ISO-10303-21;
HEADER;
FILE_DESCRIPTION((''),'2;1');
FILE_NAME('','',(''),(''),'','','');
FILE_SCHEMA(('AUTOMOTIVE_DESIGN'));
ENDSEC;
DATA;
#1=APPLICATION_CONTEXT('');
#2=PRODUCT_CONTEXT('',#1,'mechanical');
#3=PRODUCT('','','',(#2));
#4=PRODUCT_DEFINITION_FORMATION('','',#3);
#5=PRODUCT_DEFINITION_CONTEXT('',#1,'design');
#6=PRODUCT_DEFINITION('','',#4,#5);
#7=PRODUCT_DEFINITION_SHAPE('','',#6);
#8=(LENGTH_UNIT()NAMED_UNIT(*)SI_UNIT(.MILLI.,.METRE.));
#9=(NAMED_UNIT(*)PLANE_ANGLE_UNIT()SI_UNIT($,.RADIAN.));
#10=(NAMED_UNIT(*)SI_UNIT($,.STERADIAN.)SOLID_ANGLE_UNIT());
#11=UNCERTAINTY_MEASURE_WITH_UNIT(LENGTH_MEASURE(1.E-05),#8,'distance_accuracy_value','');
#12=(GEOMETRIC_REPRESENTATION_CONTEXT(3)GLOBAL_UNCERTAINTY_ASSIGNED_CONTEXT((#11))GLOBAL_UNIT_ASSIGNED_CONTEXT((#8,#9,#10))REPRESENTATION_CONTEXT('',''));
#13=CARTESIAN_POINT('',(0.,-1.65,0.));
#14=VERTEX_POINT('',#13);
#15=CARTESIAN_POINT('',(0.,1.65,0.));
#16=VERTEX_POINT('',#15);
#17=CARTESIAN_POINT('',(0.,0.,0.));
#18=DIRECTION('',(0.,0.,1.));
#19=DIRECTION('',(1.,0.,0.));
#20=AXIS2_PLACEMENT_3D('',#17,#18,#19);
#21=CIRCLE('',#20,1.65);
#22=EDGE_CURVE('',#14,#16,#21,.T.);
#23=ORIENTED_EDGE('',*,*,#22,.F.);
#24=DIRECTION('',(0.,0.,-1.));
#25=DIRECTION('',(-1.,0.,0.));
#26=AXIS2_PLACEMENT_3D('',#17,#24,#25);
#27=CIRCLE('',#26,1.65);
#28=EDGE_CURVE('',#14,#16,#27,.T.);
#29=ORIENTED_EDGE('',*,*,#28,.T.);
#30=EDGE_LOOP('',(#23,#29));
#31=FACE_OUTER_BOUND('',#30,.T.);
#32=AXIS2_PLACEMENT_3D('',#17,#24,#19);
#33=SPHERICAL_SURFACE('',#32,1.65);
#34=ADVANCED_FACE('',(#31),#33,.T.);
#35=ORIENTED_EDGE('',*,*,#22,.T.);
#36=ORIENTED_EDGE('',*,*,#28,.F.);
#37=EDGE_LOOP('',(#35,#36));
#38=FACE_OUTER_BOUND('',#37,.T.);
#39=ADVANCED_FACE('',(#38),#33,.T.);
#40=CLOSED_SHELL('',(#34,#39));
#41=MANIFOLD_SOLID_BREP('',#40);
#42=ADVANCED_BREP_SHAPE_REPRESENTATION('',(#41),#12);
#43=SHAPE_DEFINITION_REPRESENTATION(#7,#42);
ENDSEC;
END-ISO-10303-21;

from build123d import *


with BuildPart() as part:
    # Sketch1 → Revolve1 (revolve)
    with BuildSketch(Plane.XY):
        with BuildLine():
            Line((0, 1.65), (0, -1.65))
            ThreePointArc((0, -1.65), (1.65, 0), (0, 1.65))
        make_face()
    revolve(axis=Axis((0, 1.65, 0), (0, -1, 0)))


solid = part.part
